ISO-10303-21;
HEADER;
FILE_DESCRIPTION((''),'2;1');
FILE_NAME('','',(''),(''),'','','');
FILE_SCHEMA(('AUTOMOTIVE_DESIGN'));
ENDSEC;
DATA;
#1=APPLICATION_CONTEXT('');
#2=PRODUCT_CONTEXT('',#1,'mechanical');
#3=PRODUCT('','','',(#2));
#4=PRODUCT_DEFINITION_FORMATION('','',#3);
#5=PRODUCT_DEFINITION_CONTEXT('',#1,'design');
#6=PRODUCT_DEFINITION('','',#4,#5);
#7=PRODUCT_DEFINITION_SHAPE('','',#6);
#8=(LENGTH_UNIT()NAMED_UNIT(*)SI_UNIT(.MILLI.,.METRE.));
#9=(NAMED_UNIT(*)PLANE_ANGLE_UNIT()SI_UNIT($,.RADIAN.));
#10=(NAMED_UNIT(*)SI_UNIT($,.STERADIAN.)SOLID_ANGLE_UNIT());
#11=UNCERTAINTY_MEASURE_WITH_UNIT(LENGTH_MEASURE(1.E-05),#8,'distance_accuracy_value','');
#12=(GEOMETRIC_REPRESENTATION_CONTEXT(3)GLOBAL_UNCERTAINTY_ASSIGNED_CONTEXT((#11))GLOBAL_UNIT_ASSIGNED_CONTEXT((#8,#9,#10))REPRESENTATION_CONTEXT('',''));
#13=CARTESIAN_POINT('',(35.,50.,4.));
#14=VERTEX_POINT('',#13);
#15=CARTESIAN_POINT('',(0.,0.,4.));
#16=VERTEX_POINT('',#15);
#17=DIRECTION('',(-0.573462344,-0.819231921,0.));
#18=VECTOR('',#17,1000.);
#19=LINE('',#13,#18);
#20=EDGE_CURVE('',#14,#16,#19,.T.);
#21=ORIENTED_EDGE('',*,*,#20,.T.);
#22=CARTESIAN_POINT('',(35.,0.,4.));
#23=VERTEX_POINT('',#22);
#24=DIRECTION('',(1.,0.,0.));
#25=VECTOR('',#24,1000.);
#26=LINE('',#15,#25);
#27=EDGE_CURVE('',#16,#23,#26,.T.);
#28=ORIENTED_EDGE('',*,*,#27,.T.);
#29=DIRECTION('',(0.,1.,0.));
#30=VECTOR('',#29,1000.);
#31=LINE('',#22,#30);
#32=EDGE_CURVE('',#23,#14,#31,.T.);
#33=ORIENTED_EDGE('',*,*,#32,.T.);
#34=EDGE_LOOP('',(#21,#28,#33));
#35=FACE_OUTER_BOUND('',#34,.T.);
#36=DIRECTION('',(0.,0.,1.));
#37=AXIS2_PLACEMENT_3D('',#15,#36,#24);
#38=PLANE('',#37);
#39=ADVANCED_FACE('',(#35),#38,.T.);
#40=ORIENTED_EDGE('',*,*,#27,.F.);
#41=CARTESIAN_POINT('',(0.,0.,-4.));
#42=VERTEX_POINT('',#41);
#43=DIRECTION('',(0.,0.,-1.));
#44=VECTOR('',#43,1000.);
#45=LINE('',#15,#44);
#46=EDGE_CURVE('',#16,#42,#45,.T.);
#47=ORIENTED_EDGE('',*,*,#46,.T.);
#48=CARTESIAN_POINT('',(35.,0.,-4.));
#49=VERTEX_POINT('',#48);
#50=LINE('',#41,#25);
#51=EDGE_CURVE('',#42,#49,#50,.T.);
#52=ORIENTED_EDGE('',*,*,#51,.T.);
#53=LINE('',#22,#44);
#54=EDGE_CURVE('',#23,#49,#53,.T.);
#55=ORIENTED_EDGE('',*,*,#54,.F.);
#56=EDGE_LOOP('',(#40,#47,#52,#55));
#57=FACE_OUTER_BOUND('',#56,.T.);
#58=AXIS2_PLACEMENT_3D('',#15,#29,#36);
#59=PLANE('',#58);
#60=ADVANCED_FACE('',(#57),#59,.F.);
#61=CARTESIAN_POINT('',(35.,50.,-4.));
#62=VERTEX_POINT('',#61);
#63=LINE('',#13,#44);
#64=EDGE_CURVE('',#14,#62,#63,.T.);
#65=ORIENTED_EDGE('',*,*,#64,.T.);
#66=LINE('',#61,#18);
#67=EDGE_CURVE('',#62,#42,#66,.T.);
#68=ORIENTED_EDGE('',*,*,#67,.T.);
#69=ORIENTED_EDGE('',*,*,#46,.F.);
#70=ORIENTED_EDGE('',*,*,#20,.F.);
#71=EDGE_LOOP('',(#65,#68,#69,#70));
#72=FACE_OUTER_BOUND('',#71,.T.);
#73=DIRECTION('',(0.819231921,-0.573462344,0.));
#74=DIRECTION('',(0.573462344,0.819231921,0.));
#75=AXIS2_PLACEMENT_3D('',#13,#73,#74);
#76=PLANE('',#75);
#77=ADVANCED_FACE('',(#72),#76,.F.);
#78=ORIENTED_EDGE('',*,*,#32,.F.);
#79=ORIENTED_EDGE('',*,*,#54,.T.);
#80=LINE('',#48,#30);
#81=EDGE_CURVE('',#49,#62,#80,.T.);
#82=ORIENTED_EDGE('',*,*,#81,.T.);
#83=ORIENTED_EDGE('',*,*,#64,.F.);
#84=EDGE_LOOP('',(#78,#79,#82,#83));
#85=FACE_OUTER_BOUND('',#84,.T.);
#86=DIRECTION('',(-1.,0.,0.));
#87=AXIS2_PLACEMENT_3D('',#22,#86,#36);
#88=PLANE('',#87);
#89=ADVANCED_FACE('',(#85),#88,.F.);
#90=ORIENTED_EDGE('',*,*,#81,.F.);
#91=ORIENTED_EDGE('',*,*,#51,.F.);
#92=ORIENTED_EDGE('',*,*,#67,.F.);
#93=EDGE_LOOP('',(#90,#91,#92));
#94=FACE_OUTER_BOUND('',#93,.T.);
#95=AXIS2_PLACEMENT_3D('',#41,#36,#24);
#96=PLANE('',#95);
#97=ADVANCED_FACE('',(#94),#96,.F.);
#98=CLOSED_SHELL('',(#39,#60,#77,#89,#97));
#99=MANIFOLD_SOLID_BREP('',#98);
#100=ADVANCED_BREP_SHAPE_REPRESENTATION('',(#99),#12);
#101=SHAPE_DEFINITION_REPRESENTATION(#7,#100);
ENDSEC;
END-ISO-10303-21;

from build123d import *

# Parameters (mm, degrees)
EXTRUDE_1_DEPTH = 4


with BuildPart() as part:
    # 草图1 → 凸台-拉伸1 (new, symmetric)
    with BuildSketch(Plane.XY):
        Polygon((0, 0), (35, 0), (35, 50), align=None)
    extrude(amount=EXTRUDE_1_DEPTH, both=True)


solid = part.part
